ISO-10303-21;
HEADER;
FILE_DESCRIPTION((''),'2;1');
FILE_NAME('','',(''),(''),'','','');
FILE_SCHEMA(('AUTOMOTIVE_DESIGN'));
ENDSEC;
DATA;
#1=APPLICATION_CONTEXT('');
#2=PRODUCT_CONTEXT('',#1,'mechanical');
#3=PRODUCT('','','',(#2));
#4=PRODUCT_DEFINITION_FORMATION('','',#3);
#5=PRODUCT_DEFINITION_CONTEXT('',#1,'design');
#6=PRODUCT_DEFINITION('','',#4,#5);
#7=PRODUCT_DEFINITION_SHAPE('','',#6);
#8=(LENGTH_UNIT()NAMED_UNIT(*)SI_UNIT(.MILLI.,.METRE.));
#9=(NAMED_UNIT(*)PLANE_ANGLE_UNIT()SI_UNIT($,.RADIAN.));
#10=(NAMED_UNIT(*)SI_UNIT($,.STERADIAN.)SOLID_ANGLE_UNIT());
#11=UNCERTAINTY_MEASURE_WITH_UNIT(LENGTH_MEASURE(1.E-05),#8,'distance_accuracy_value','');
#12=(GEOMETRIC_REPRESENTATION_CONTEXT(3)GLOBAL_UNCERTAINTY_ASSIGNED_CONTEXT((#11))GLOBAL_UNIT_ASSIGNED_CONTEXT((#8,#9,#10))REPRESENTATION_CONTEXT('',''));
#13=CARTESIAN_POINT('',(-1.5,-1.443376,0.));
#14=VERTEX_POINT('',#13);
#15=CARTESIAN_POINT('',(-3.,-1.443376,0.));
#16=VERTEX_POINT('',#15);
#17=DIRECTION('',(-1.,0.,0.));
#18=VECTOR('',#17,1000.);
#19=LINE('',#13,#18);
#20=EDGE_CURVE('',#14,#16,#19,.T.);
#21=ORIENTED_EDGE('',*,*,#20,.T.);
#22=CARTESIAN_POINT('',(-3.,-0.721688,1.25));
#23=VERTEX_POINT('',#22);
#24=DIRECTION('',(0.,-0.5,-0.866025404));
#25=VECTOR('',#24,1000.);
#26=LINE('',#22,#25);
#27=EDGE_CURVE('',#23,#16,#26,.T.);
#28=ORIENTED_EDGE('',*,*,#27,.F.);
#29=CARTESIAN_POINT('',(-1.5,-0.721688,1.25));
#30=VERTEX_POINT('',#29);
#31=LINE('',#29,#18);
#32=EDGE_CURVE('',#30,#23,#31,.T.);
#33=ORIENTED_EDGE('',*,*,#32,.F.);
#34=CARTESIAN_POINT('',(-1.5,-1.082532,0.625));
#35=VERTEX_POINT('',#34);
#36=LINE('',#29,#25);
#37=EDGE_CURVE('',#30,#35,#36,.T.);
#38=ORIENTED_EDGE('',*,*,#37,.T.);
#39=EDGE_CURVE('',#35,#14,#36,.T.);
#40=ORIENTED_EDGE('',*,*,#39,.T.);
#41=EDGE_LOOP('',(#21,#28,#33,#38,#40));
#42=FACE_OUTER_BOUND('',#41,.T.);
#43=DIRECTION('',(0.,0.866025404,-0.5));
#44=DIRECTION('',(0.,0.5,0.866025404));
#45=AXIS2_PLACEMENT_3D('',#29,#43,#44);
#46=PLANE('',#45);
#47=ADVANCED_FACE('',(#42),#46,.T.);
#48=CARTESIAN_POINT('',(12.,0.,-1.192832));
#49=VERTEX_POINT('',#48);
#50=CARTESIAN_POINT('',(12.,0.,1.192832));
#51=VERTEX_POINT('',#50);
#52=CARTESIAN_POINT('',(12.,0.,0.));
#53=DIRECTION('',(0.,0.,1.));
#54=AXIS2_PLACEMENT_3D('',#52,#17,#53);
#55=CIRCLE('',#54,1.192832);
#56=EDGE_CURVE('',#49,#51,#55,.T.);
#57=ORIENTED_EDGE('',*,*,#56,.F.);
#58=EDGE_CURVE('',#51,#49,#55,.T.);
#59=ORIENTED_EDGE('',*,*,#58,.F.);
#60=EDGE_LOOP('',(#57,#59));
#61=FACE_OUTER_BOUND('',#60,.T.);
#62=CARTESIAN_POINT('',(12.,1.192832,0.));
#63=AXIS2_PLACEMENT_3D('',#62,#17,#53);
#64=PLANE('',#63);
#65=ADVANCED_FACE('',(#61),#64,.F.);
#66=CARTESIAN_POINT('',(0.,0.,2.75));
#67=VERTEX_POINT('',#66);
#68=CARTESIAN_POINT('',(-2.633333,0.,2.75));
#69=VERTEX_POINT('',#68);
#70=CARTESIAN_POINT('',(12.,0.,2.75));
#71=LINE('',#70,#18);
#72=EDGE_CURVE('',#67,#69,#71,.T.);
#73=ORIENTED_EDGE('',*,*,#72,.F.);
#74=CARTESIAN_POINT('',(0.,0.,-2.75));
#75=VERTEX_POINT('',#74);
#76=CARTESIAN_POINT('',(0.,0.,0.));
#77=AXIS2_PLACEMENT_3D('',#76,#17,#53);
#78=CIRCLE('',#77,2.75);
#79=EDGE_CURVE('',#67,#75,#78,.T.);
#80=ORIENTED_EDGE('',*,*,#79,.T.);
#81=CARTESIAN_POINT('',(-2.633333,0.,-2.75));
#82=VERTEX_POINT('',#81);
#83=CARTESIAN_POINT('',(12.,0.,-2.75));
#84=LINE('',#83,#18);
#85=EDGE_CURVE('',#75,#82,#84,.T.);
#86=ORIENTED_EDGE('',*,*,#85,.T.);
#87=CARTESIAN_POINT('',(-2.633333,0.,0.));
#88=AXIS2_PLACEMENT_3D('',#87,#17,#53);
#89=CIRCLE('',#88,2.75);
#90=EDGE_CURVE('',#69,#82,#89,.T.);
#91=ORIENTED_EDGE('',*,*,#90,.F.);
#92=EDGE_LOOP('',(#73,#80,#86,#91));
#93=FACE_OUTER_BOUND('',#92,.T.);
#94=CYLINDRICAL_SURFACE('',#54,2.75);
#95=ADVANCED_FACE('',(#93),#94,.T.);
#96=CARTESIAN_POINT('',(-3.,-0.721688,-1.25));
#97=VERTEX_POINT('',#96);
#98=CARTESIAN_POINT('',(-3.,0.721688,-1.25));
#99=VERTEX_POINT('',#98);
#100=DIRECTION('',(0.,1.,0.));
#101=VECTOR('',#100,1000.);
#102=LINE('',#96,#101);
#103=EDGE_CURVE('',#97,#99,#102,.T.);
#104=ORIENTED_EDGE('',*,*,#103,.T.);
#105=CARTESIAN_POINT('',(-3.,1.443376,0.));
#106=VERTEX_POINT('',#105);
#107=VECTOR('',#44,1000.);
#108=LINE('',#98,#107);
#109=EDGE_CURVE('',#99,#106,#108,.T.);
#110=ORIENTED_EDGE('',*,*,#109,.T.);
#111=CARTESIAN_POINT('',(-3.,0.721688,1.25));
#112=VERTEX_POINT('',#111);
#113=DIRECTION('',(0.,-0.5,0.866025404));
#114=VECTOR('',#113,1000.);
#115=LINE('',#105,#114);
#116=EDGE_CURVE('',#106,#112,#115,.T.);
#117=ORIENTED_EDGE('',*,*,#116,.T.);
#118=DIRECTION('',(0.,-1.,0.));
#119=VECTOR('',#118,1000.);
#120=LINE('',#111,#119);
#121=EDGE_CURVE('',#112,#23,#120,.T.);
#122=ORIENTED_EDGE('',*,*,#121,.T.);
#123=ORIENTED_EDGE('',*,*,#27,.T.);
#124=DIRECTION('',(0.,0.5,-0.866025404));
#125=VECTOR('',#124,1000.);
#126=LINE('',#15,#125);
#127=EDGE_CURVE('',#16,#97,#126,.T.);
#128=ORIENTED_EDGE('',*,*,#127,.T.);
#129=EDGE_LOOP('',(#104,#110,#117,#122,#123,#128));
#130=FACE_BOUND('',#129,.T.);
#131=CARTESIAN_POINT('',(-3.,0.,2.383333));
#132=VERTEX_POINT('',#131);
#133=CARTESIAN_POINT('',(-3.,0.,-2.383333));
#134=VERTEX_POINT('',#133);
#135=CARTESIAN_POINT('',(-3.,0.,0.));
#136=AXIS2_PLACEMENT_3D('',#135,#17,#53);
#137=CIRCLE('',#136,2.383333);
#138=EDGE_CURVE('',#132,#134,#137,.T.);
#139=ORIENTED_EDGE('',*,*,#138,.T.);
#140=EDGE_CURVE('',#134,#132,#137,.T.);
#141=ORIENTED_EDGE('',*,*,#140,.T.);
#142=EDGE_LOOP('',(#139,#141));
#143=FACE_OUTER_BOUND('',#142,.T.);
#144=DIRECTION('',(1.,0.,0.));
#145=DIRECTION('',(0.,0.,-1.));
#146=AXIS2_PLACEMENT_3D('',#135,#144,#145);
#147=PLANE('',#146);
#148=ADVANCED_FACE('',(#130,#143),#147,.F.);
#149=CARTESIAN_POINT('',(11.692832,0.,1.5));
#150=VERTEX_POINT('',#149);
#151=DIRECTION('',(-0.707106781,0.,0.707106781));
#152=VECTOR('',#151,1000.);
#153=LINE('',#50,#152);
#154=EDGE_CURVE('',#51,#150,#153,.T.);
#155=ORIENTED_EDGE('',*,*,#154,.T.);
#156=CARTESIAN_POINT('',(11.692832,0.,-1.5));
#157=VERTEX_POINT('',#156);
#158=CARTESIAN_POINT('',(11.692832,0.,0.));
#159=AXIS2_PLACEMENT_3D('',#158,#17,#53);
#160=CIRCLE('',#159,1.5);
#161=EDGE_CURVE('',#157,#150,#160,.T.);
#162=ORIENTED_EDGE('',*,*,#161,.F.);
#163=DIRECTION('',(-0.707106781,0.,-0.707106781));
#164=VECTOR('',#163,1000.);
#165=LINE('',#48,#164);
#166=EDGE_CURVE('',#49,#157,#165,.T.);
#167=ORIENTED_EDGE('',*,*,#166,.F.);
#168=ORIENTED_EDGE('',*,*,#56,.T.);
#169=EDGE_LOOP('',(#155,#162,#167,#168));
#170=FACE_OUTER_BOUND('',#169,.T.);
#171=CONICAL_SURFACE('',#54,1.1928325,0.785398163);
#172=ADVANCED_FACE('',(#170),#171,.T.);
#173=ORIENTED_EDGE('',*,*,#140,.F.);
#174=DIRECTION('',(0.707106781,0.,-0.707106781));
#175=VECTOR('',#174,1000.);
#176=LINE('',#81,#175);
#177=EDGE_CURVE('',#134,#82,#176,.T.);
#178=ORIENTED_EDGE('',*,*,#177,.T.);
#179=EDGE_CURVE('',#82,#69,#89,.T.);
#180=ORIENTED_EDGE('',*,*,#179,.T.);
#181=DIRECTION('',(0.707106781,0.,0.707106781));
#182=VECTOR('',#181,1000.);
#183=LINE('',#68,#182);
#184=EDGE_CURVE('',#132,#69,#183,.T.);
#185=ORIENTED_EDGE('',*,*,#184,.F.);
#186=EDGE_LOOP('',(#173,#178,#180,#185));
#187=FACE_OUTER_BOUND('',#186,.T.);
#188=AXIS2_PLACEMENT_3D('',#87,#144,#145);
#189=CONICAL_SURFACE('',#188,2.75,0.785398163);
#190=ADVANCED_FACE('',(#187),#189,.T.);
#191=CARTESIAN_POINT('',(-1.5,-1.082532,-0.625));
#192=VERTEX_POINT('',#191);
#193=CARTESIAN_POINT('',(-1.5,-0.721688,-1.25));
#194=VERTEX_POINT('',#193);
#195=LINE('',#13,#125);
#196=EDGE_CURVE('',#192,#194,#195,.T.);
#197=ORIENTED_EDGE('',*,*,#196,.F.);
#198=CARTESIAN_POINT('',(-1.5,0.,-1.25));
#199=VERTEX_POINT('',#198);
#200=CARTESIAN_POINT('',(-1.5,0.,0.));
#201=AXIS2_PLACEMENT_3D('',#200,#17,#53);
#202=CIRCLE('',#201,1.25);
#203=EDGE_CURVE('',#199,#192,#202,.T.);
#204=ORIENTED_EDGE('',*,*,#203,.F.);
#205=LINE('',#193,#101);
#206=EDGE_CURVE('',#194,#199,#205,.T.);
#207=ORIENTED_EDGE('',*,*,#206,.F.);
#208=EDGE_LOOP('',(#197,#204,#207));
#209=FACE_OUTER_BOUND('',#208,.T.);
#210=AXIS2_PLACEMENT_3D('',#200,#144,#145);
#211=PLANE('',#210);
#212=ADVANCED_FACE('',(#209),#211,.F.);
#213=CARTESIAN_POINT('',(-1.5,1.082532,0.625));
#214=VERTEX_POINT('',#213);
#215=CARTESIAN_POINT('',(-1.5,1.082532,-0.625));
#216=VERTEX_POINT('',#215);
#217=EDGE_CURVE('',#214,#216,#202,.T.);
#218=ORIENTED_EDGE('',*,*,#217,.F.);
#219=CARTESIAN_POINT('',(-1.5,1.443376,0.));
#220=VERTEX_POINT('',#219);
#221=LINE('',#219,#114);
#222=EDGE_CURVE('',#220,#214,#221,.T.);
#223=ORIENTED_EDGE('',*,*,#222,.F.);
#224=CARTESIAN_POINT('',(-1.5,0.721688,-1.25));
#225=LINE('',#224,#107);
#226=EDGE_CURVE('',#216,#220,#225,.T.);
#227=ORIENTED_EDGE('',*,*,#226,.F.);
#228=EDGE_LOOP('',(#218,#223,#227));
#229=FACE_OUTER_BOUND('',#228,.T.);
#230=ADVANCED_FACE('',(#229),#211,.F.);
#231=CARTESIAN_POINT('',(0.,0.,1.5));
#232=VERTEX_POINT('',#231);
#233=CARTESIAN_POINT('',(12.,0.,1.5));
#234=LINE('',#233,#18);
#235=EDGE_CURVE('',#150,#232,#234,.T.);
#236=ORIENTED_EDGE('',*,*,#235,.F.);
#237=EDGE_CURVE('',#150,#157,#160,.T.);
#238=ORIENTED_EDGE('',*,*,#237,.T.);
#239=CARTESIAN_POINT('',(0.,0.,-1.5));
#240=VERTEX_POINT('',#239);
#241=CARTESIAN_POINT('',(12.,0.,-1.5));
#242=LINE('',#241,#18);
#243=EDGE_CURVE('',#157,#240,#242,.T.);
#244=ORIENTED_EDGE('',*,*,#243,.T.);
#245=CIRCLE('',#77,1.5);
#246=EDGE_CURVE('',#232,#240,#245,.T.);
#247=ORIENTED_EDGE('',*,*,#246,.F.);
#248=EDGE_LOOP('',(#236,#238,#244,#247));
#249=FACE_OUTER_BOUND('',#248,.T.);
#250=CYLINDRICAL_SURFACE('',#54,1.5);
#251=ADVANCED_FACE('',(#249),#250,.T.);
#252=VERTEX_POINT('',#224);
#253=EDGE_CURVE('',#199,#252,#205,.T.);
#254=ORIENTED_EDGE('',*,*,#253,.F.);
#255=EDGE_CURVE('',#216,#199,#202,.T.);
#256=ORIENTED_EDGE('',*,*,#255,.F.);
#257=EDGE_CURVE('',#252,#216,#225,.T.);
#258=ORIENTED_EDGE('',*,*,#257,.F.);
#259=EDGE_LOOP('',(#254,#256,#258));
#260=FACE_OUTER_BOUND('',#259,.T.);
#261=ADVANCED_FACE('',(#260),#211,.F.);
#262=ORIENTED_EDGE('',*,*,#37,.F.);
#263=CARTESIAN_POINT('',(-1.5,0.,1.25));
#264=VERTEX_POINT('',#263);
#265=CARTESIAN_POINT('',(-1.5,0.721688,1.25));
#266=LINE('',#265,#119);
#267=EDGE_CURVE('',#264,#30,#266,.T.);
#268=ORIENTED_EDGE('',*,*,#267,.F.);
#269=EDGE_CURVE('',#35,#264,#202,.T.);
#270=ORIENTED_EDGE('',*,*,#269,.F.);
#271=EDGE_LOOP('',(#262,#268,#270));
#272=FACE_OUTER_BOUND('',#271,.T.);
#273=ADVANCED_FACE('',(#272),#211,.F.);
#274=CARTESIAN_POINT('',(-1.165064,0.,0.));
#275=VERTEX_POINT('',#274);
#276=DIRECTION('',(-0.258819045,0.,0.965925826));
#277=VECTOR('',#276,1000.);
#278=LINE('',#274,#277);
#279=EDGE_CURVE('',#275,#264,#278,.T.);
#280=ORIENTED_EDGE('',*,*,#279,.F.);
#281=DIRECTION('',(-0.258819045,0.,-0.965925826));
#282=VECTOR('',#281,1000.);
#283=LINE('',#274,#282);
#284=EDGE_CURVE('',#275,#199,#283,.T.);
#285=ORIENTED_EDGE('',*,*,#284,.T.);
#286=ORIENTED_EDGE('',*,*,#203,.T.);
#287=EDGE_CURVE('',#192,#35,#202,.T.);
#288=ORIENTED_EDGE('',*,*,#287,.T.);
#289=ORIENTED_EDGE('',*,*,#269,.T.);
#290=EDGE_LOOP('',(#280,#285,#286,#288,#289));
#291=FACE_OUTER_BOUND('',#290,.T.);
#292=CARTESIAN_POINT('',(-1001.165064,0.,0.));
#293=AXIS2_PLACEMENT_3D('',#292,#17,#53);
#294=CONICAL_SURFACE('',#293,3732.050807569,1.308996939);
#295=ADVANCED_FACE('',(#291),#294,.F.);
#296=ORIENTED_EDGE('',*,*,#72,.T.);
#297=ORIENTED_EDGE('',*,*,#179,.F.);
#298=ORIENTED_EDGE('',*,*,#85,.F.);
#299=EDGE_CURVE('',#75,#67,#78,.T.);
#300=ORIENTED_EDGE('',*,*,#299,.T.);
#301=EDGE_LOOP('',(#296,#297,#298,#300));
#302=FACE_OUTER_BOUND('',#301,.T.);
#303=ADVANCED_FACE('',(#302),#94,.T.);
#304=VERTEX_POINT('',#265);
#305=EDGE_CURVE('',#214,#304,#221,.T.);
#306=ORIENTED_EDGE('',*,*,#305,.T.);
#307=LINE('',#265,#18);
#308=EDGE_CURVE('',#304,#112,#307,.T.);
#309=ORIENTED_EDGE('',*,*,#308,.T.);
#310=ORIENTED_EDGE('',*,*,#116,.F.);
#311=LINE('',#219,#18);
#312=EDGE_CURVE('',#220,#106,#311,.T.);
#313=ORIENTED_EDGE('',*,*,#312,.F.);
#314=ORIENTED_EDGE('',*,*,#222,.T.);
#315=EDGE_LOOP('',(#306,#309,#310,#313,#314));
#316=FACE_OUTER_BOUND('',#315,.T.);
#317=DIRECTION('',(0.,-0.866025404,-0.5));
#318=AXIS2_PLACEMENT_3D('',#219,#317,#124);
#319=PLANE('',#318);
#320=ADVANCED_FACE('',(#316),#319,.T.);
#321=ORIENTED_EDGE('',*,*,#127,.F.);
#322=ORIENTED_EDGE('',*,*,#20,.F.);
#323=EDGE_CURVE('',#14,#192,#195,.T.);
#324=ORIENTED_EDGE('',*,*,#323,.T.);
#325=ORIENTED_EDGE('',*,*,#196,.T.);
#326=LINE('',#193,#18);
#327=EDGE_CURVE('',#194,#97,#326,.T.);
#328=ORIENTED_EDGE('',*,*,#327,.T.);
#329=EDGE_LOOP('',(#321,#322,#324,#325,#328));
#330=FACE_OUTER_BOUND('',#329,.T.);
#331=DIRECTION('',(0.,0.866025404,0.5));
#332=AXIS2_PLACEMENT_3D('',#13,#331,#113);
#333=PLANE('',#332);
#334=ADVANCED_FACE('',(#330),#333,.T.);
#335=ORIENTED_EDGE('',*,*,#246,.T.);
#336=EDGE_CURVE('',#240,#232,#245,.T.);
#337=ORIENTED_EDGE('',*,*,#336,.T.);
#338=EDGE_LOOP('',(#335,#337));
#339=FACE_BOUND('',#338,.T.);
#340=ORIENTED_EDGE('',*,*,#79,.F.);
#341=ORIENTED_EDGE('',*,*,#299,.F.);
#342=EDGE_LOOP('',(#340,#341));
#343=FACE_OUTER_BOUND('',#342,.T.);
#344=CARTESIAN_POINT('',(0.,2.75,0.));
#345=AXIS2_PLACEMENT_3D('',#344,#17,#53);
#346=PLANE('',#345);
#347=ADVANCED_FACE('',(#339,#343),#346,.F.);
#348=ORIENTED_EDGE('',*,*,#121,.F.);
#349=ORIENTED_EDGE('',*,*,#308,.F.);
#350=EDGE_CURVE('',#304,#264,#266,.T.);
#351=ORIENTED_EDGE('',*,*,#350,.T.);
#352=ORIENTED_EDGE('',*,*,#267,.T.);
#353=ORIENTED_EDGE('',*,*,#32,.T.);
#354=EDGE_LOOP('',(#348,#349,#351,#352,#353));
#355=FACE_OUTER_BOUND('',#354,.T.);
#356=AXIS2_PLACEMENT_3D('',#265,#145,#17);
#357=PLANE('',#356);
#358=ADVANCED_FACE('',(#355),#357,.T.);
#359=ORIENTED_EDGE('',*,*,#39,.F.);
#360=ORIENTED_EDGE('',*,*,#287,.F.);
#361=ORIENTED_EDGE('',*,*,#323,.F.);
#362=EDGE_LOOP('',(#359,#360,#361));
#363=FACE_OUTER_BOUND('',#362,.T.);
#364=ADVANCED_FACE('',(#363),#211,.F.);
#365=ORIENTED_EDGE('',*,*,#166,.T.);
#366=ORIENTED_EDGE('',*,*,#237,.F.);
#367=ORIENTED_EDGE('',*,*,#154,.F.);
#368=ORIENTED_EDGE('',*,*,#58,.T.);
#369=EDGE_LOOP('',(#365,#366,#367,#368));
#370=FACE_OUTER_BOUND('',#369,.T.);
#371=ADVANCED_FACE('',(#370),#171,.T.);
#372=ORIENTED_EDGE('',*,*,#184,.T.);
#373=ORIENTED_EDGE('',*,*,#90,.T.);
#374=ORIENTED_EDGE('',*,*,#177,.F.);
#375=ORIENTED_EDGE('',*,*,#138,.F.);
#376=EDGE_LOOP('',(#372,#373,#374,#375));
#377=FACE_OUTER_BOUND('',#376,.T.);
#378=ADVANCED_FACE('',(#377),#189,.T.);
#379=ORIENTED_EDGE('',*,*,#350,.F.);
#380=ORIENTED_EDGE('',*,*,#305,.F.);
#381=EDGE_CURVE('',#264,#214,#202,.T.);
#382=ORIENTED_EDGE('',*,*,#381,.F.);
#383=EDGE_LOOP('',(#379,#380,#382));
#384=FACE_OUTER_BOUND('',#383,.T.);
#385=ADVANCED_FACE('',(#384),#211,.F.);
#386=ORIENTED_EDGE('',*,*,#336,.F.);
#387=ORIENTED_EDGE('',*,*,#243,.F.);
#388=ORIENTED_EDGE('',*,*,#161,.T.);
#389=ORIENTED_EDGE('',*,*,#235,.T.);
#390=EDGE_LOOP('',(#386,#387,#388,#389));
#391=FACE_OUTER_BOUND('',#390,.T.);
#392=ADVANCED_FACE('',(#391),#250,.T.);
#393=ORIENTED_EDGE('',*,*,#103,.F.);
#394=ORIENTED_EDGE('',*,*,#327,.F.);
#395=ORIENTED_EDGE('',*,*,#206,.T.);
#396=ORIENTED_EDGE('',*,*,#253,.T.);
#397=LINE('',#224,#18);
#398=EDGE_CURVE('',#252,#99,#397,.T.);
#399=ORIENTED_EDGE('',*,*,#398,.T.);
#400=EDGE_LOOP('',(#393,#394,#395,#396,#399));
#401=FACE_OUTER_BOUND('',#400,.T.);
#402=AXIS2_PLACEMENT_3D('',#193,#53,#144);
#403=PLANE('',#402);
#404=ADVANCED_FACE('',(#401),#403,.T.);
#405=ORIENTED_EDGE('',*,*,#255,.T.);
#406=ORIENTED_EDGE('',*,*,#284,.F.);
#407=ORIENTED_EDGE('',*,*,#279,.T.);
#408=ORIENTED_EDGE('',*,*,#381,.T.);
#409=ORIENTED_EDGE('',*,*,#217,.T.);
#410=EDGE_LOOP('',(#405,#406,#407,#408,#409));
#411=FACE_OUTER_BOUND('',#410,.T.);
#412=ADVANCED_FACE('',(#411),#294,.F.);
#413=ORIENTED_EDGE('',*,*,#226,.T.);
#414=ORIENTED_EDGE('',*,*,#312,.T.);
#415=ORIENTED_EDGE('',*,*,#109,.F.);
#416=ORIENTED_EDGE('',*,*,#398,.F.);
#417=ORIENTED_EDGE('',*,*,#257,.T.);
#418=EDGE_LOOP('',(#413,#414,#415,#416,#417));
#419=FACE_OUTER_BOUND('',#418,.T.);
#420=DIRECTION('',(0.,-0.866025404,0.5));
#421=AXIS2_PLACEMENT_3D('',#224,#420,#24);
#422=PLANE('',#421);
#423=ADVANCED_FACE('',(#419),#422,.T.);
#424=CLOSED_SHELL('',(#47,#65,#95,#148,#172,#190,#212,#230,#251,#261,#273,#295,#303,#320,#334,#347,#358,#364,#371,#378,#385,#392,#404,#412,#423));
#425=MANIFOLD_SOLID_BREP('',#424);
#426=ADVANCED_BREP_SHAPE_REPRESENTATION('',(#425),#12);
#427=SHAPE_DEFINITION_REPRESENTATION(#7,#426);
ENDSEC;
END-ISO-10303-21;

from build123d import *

# Parameters (mm, degrees)
CUT_EXTRUDE1_DEPTH = 1.5


with BuildPart() as part:
    # Sketch1 → Revolve1 (revolve)
    with BuildSketch(Plane.XY, mode=Mode.PRIVATE) as revolve1_sk:
        Polygon((-3, 0), (-3, 2.383333333), (-2.633333333, 2.75), (0, 2.75), (0, 1.5), (11.6928325, 1.5), (12, 1.1928325), (12, 0), align=None)
    revolve(revolve1_sk.sketch.rotate(Axis((12, 0, 0), (-1, 0, 0)), 270), axis=Axis((12, 0, 0), (-1, 0, 0)))

    # Sketch2 → Cut-Revolve1 (revolve, cut)
    with BuildSketch(Plane.XY, mode=Mode.PRIVATE) as cut_revolve1_sk:
        Polygon((-3, 0), (-3, 1.25), (-1.5, 1.25), (-1.165063509, 0), align=None)
    revolve(cut_revolve1_sk.sketch.rotate(Axis((-1.165063509, 0, 0), (-1, 0, 0)), 270), axis=Axis((-1.165063509, 0, 0), (-1, 0, 0)), mode=Mode.SUBTRACT)

    # Sketch3 → Cut-Extrude1 (cut)
    with BuildSketch(Plane(origin=(-3, 0, 0), x_dir=(0, 0, -1), z_dir=(1, 0, 0))):
        Polygon((-1.25, 0.721687836), (-1.25, -0.721687836), (0, -1.443375673), (1.25, -0.721687836), (1.25, 0.721687836), (0, 1.443375673), align=None)
    extrude(amount=CUT_EXTRUDE1_DEPTH, mode=Mode.SUBTRACT)


solid = part.part
